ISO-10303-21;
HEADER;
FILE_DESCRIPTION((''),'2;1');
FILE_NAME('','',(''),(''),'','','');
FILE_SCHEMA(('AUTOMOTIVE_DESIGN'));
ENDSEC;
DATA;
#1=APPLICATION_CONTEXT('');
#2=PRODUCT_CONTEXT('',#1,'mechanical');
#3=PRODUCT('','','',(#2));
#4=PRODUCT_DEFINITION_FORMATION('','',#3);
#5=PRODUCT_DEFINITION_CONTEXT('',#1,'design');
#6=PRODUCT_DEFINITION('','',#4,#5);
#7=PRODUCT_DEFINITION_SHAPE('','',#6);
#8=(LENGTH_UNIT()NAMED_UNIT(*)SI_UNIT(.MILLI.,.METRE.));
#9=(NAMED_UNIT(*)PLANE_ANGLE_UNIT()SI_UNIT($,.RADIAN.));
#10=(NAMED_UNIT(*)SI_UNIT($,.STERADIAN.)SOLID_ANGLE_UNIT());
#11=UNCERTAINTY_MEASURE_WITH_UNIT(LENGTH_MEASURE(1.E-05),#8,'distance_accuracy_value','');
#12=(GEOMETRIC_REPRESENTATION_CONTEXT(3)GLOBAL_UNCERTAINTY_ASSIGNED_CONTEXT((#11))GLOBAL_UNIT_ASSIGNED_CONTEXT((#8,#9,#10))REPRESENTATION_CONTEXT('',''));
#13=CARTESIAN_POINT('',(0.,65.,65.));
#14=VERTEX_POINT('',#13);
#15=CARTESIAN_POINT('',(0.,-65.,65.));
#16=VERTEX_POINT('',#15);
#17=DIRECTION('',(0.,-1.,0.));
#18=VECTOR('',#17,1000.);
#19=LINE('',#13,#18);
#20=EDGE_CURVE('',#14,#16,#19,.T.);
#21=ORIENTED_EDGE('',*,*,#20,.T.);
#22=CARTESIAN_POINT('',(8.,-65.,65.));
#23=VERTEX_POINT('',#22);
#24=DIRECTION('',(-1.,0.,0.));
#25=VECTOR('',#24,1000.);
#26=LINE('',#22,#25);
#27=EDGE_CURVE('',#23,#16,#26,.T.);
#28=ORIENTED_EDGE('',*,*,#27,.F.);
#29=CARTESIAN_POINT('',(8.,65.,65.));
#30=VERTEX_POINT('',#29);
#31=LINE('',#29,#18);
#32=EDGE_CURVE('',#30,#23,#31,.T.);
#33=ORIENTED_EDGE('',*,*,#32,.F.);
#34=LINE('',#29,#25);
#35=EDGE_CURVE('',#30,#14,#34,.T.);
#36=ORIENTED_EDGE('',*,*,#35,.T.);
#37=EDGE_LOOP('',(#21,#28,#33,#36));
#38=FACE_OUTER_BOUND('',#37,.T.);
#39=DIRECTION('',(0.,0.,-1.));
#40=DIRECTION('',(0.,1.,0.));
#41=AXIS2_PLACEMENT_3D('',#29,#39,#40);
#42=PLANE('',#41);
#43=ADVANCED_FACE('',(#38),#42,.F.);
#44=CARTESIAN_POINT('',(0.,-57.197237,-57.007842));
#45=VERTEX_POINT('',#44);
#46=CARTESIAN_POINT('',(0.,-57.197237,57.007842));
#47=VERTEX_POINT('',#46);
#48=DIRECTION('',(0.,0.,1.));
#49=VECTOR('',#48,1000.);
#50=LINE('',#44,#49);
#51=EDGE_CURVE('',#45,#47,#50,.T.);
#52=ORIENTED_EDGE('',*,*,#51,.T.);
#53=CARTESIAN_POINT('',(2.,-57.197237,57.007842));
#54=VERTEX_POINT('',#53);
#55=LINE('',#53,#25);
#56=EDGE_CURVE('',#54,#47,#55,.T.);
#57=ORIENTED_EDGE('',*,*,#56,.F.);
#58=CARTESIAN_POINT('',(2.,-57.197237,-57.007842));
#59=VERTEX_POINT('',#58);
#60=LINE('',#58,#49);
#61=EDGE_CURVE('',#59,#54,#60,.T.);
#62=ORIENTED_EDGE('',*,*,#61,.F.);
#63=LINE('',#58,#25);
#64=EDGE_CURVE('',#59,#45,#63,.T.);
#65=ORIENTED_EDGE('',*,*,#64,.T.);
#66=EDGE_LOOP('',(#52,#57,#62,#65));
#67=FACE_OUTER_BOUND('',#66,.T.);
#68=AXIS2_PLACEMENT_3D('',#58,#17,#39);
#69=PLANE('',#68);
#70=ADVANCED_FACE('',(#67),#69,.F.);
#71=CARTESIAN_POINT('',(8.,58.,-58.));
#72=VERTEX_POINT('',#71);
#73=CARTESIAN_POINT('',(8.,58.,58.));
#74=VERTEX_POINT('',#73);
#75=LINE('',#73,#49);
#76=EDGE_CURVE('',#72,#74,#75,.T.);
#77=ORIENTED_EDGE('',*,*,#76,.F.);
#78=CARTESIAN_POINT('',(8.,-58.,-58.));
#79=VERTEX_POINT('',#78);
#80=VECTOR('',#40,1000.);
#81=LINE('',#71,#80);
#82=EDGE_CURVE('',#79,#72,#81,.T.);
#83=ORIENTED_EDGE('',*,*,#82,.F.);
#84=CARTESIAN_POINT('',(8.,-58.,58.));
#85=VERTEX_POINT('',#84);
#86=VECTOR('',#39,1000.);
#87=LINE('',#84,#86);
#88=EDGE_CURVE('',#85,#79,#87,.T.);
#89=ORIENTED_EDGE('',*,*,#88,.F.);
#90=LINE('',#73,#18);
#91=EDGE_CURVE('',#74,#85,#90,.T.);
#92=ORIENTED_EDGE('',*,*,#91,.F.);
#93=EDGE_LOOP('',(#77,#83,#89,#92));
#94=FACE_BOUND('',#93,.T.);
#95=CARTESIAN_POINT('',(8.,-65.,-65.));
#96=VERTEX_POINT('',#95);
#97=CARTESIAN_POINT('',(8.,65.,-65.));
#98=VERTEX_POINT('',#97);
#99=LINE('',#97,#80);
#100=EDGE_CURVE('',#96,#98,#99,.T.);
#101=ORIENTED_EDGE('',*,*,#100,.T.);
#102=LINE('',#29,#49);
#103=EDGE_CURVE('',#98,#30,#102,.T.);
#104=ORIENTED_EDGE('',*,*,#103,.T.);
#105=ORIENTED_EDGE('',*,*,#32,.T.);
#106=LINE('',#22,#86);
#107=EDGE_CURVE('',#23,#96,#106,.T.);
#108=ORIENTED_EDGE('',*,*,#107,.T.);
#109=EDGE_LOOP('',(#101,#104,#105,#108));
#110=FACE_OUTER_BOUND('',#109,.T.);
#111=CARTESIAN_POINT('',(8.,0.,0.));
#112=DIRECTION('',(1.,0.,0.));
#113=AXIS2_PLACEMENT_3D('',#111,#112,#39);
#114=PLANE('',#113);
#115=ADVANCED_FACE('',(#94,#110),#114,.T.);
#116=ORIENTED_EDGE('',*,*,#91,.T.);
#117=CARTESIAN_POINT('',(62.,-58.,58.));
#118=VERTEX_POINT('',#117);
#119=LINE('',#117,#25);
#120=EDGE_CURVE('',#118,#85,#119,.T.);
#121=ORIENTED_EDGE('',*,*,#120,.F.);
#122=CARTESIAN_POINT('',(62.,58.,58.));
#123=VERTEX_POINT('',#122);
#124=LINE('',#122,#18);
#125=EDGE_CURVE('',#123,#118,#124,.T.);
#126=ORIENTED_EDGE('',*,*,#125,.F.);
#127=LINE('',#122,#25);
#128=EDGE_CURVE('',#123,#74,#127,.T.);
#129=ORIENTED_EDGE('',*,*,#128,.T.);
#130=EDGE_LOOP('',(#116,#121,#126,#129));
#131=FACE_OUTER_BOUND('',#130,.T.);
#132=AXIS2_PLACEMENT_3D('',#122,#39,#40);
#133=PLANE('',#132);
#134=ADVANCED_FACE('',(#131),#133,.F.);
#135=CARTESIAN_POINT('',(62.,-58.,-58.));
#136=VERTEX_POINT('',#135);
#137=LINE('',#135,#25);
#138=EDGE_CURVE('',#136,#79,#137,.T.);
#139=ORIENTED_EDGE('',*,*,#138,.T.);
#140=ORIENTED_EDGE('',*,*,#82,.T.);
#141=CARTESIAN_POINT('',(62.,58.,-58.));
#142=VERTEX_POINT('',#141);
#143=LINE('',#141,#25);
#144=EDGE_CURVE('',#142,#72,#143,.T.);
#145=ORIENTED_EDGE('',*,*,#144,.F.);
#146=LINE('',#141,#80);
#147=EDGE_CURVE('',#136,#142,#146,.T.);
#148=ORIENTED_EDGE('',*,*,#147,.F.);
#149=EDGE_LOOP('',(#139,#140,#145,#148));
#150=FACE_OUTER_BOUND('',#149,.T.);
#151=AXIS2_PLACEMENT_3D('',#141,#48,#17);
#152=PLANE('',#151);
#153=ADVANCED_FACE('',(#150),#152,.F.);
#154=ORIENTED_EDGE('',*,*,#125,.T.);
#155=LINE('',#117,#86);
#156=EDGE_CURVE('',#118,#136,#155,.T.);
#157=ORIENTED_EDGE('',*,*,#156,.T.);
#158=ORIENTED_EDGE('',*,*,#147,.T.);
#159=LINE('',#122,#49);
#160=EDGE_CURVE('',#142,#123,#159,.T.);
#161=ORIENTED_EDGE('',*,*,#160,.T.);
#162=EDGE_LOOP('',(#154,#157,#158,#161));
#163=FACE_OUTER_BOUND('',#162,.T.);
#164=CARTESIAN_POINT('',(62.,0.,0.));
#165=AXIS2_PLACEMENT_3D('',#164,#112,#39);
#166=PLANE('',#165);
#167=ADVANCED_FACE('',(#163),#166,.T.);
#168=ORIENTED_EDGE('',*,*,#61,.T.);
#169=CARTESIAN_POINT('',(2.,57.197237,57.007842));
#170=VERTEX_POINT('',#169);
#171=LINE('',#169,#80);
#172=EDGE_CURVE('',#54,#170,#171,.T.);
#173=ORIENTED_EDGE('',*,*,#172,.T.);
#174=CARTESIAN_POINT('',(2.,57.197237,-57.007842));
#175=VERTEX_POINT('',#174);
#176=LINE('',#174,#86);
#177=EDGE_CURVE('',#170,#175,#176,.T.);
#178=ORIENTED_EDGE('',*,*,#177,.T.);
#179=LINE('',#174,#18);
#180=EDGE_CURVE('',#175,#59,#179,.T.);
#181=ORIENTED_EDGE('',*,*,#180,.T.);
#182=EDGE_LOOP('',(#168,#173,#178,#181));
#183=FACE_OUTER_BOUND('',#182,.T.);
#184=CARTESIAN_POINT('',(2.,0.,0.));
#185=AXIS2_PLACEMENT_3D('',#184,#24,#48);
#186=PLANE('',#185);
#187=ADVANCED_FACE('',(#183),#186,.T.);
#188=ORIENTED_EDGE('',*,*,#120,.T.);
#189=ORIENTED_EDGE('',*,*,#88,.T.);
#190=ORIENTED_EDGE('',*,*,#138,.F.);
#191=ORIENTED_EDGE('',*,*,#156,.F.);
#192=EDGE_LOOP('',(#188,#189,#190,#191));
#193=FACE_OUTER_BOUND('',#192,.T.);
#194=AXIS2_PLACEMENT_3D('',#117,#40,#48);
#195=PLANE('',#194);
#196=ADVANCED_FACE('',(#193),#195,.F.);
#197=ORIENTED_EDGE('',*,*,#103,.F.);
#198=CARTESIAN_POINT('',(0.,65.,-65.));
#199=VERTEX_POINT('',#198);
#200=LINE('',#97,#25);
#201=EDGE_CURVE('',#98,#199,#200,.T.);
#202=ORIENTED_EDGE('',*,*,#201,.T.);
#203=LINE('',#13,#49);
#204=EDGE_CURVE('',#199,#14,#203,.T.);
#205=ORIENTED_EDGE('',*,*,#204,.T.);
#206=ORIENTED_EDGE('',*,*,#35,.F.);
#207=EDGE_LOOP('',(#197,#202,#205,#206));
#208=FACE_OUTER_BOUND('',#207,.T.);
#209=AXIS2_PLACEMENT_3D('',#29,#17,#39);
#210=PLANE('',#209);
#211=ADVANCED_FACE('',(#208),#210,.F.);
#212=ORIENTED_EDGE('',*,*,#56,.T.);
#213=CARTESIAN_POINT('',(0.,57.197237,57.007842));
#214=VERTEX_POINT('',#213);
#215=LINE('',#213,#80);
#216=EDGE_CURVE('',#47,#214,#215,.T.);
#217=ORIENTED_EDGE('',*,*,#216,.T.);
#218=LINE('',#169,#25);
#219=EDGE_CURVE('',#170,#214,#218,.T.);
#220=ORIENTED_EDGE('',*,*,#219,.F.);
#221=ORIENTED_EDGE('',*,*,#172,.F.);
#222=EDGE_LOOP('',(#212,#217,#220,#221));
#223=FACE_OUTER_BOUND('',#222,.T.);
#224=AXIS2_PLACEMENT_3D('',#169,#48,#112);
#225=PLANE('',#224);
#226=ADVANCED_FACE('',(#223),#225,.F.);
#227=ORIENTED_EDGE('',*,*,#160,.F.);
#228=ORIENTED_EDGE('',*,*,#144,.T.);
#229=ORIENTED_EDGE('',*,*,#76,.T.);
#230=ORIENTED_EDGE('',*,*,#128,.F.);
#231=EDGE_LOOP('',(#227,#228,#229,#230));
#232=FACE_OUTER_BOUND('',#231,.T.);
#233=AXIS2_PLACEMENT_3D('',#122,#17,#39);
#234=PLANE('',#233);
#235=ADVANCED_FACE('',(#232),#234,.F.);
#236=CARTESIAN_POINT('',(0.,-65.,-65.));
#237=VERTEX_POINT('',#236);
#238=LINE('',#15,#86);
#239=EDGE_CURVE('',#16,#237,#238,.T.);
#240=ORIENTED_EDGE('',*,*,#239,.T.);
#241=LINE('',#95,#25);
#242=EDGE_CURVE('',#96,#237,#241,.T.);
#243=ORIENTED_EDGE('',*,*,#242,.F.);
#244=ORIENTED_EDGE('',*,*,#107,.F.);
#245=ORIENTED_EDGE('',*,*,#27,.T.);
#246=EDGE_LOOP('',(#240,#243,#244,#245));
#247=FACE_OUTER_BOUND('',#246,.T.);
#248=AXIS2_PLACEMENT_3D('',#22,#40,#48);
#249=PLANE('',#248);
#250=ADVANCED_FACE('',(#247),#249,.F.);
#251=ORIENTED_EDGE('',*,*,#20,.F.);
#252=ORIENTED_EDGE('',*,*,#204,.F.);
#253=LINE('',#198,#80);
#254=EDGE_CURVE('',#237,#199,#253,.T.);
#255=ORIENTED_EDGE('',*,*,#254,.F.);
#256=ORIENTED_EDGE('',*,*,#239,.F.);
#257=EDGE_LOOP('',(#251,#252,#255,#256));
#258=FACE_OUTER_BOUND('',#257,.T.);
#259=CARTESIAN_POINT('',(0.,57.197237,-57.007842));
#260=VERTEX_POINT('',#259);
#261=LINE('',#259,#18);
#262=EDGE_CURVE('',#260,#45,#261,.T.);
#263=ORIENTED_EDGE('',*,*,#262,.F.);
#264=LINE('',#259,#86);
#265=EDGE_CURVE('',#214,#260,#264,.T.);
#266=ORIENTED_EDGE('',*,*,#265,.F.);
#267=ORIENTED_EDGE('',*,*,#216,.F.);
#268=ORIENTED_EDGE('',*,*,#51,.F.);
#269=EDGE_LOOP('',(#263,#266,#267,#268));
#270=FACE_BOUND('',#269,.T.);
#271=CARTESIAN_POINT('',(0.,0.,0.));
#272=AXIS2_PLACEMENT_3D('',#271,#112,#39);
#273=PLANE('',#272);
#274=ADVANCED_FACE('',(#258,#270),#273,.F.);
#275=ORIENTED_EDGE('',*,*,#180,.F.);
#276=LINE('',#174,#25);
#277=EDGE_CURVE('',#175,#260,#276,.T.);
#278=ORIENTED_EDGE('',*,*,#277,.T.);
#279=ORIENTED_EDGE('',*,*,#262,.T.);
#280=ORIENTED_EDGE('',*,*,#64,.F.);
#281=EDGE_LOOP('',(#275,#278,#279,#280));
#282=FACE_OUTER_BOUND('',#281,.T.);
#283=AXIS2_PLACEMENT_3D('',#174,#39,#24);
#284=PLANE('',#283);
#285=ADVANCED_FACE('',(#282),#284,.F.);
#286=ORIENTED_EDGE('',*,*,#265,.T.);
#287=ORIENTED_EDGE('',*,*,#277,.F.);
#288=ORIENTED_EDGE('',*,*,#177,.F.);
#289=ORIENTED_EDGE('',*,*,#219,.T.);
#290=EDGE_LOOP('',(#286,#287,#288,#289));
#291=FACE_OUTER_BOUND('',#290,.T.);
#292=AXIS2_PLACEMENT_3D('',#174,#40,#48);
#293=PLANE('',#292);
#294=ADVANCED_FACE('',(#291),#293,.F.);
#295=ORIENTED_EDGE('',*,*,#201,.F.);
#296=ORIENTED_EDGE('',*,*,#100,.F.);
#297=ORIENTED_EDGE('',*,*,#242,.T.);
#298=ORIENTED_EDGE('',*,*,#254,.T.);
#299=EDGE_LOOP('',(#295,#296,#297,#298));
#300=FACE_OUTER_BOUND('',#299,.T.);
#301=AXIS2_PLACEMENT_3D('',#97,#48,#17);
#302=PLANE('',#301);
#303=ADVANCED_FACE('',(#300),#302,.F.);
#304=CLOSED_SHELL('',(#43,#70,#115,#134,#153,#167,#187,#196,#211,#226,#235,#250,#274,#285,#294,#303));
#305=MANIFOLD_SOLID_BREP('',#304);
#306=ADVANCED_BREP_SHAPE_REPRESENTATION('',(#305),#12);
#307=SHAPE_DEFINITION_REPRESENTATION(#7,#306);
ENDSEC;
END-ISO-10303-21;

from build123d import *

# Parameters (mm, degrees)
SKETCH_1_W          = 130
SKETCH_1_H          = 130
EXTRUDE_1_DEPTH     = 8
SKETCH_2_W          = 116
SKETCH_2_H          = 116
EXTRUDE_2_DEPTH     = 54
SKETCH_3_W          = 114.015684478
SKETCH_3_H          = 114.394474128
CUT_EXTRUDE_1_DEPTH = 2


with BuildPart() as part:
    # 草图1 → 凸台-拉伸1 (new body)
    with BuildSketch(Plane(origin=(0, 0, 0), x_dir=(0, 0, -1), z_dir=(1, 0, 0))):
        Rectangle(SKETCH_1_W, SKETCH_1_H)
    extrude(amount=EXTRUDE_1_DEPTH)

    # 草图2 → 凸台-拉伸2 (add)
    with BuildSketch(Plane(origin=(8, 0, 0), x_dir=(0, 0, -1), z_dir=(1, 0, 0))):
        Rectangle(SKETCH_2_W, SKETCH_2_H)
    extrude(amount=EXTRUDE_2_DEPTH)

    # 草图3 → 切除-拉伸1 (cut)
    with BuildSketch(Plane.ZY):
        Rectangle(SKETCH_3_W, SKETCH_3_H)
    extrude(amount=-CUT_EXTRUDE_1_DEPTH, mode=Mode.SUBTRACT)


solid = part.part
